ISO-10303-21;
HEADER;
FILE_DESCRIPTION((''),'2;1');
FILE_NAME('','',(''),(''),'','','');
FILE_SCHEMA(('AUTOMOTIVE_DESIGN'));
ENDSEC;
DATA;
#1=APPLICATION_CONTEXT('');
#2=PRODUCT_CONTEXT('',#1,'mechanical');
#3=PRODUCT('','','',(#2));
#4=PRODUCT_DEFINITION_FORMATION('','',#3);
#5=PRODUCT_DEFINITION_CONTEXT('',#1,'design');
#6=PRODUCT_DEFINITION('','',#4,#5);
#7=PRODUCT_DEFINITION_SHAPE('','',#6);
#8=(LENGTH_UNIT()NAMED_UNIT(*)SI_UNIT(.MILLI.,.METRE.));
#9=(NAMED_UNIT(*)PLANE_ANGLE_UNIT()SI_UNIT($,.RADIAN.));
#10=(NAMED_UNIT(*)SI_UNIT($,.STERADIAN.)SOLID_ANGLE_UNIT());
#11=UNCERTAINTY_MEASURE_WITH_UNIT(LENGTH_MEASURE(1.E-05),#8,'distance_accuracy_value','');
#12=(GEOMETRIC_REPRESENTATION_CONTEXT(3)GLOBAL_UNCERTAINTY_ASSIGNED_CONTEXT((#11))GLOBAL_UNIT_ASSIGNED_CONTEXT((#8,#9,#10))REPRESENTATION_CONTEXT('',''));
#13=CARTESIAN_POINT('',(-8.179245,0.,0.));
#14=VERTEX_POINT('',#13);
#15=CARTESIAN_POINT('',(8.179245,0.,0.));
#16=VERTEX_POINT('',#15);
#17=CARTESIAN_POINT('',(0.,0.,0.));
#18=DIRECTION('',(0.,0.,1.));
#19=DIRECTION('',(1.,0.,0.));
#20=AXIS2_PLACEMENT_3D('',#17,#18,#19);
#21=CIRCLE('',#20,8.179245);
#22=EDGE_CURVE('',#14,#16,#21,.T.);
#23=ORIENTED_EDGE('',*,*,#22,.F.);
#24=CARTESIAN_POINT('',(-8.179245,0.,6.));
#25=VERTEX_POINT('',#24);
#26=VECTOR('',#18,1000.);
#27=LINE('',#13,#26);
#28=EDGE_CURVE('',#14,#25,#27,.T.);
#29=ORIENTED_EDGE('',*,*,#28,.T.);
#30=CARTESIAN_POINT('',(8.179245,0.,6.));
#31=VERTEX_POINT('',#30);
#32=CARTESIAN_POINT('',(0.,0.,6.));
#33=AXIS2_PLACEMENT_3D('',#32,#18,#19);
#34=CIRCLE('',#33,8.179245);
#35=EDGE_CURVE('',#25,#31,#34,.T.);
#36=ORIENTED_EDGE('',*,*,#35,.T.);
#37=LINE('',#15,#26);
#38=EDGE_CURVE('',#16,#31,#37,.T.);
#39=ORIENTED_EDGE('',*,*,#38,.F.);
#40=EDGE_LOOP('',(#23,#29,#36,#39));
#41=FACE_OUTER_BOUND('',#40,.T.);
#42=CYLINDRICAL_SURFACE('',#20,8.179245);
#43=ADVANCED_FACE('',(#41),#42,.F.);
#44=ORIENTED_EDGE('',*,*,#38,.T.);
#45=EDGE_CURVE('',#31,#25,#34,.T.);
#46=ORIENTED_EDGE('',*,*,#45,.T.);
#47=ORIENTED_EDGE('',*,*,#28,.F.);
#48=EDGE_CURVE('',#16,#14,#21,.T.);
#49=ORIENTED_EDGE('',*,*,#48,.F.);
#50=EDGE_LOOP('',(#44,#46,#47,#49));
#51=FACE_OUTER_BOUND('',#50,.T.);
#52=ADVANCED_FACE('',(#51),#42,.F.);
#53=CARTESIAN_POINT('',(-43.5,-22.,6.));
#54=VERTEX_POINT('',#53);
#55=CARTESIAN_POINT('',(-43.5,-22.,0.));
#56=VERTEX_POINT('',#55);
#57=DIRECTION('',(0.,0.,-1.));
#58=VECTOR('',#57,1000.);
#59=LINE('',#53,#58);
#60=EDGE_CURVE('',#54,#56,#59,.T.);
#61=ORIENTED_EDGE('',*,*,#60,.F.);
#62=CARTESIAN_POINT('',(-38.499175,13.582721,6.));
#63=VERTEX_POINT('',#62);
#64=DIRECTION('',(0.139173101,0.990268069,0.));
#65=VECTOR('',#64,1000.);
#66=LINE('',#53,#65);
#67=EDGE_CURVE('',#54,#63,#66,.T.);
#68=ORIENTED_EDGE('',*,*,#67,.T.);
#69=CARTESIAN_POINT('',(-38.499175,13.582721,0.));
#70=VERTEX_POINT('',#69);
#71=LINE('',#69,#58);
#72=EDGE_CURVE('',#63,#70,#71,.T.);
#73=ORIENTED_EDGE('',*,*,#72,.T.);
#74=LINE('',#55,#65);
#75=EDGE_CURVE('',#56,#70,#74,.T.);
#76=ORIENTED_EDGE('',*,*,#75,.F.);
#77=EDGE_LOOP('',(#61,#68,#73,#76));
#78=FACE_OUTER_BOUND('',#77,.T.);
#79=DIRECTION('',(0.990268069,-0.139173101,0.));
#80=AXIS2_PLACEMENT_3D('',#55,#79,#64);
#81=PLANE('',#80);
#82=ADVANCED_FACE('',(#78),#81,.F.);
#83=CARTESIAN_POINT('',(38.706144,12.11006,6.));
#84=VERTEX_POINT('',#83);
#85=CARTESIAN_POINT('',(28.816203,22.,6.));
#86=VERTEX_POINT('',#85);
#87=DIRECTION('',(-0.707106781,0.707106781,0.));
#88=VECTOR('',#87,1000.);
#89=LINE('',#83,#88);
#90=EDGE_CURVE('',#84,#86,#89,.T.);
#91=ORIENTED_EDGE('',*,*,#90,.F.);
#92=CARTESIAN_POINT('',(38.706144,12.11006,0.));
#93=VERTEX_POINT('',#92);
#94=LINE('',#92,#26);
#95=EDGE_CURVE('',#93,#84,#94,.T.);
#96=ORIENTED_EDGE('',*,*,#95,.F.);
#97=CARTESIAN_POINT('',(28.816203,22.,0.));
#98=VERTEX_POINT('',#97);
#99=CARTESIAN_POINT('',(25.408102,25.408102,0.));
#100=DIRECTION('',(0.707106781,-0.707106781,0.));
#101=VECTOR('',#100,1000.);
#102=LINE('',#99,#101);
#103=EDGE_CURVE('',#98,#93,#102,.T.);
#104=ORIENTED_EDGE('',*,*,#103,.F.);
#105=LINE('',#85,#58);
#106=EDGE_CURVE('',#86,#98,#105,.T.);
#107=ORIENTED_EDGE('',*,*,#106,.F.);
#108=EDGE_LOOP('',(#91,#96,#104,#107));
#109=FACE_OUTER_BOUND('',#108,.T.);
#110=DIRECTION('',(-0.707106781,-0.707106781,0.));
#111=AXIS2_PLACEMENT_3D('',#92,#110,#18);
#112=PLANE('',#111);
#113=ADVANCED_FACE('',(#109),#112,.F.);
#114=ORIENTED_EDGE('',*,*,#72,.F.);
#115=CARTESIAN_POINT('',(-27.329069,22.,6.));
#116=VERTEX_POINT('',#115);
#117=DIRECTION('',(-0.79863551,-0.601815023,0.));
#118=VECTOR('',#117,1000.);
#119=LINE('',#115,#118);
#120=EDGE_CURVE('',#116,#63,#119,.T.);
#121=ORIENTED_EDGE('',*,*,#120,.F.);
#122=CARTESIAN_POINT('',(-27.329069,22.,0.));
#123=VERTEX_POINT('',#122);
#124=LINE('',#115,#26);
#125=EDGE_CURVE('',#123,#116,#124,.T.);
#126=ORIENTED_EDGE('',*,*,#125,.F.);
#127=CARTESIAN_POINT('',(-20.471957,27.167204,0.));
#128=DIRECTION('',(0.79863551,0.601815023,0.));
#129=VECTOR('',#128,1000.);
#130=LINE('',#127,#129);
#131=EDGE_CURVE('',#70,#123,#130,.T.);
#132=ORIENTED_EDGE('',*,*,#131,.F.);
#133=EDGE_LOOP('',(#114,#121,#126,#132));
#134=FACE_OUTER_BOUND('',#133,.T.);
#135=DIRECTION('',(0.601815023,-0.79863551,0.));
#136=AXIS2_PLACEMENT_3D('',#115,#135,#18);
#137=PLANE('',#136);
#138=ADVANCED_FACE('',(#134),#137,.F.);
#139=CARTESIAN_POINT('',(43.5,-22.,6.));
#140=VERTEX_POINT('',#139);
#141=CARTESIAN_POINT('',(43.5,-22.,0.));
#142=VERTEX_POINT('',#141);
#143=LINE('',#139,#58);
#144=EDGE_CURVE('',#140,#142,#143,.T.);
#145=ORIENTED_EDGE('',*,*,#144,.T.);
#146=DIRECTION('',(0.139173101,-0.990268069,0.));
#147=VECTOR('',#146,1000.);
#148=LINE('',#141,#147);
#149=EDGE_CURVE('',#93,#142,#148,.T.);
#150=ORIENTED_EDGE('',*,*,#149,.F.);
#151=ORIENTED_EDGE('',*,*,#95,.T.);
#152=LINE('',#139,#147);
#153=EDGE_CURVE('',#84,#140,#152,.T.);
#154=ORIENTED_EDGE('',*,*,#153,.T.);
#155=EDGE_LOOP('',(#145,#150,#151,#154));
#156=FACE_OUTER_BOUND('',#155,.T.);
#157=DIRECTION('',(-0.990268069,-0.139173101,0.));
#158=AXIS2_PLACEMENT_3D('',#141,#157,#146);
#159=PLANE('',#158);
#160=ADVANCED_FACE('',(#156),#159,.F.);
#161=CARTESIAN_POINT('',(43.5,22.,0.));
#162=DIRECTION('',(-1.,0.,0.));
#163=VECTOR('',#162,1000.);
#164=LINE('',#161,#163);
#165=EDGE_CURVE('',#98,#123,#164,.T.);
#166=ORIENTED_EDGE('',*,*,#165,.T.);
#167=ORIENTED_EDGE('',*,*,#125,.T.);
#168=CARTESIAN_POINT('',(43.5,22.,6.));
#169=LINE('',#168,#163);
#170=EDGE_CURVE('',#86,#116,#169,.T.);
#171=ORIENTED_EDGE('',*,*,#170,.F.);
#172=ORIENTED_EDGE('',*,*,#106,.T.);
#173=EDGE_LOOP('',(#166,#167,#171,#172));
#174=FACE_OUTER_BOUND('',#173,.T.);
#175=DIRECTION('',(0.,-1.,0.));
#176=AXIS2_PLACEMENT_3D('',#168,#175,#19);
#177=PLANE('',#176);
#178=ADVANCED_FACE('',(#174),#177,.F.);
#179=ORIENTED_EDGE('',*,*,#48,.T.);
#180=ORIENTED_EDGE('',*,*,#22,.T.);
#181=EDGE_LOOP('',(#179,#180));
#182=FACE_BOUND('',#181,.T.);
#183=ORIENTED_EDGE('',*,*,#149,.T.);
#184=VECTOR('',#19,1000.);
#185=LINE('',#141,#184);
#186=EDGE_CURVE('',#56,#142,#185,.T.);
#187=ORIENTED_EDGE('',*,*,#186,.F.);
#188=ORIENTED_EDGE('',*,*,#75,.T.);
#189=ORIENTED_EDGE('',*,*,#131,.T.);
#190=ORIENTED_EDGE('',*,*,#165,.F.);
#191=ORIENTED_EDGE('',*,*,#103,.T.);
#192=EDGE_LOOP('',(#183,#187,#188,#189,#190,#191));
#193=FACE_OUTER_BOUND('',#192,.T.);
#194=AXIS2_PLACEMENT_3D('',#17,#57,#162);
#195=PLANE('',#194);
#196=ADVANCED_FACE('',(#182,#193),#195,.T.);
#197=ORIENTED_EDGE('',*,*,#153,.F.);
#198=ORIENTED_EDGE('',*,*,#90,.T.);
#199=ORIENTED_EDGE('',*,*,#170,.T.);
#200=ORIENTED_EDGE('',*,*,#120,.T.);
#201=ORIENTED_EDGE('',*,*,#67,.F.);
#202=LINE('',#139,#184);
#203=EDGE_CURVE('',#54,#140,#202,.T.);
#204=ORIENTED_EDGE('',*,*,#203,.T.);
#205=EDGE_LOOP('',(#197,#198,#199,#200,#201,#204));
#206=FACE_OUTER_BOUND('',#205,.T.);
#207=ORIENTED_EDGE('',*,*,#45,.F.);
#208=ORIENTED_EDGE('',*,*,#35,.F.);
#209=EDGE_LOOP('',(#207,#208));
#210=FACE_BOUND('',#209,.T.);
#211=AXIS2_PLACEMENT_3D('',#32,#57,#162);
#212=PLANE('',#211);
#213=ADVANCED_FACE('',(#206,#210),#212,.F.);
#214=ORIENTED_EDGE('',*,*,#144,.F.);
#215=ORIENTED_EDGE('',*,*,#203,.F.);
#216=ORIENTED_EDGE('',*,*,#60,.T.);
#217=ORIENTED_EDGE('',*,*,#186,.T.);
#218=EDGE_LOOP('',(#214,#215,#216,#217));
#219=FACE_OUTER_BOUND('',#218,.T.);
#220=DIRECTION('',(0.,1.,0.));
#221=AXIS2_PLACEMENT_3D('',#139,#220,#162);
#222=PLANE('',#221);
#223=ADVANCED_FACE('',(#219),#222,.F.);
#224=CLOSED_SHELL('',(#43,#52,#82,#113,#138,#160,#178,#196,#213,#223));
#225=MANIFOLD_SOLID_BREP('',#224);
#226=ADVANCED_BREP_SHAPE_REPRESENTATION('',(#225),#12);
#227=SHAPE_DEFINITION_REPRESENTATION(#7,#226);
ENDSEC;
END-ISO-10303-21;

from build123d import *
from OCP.BRepFilletAPI import BRepFilletAPI_MakeChamfer

# Parameters (mm, degrees)
SKETCH_1_W          = 87
SKETCH_1_H          = 44
EXTRUDE_1_DEPTH     = 6
SKETCH_2_R          = 8.179245246
CUT_EXTRUDE_1_DEPTH = 6
CHAMFER_1_SIZE      = 8.5
CHAMFER_1_SIZE2     = 9.987134599


with BuildPart() as part:
    # 草图1 → 凸台-拉伸1 (new body)
    with BuildSketch(Plane.XY):
        Rectangle(SKETCH_1_W, SKETCH_1_H)
    extrude(amount=EXTRUDE_1_DEPTH)

    # 草图2 → 切除-拉伸1 (cut)
    with BuildSketch(Plane.XY.offset(6)):
        Circle(SKETCH_2_R)
        Polygon((-43.5, -22), (-37.316203273, 22), (-43.5, 22), align=None)
        Polygon((43.5, -22), (37.316203273, 22), (43.5, 22), align=None)
    extrude(amount=-CUT_EXTRUDE_1_DEPTH, mode=Mode.SUBTRACT)

    # 倒角1: one chamfer whose edges measure the first distance from different faces: ONE call of the kernel's chamfer builder (chamfer() names one face for all edges)
    chamfer_1_edges_1 = [part.edges().sort_by_distance(p)[0] for p in [
        (37.316203273, 22, 3),
    ]]
    chamfer_1_side_1 = [part.faces().sort_by_distance(p)[0] for p in [
        (0, 22, 3),
    ]]
    chamfer_1_edges_2 = [part.edges().sort_by_distance(p)[0] for p in [
        (-37.316203273, 22, 3),
    ]]
    chamfer_1_side_2 = [part.faces().sort_by_distance(p)[0] for p in [
        (-40.408101637, 0, 3),
    ]]
    chamfer_1 = BRepFilletAPI_MakeChamfer(part.part.solid().wrapped)
    for e in chamfer_1_edges_1:
        chamfer_1.Add(CHAMFER_1_SIZE, CHAMFER_1_SIZE2, e.wrapped, chamfer_1_side_1[0].wrapped)  # the first distance lies on this face
    for e in chamfer_1_edges_2:
        chamfer_1.Add(CHAMFER_1_SIZE, CHAMFER_1_SIZE2, e.wrapped, chamfer_1_side_2[0].wrapped)  # the first distance lies on this face
    add(Compound.cast(chamfer_1.Shape()), mode=Mode.REPLACE)


solid = part.part
